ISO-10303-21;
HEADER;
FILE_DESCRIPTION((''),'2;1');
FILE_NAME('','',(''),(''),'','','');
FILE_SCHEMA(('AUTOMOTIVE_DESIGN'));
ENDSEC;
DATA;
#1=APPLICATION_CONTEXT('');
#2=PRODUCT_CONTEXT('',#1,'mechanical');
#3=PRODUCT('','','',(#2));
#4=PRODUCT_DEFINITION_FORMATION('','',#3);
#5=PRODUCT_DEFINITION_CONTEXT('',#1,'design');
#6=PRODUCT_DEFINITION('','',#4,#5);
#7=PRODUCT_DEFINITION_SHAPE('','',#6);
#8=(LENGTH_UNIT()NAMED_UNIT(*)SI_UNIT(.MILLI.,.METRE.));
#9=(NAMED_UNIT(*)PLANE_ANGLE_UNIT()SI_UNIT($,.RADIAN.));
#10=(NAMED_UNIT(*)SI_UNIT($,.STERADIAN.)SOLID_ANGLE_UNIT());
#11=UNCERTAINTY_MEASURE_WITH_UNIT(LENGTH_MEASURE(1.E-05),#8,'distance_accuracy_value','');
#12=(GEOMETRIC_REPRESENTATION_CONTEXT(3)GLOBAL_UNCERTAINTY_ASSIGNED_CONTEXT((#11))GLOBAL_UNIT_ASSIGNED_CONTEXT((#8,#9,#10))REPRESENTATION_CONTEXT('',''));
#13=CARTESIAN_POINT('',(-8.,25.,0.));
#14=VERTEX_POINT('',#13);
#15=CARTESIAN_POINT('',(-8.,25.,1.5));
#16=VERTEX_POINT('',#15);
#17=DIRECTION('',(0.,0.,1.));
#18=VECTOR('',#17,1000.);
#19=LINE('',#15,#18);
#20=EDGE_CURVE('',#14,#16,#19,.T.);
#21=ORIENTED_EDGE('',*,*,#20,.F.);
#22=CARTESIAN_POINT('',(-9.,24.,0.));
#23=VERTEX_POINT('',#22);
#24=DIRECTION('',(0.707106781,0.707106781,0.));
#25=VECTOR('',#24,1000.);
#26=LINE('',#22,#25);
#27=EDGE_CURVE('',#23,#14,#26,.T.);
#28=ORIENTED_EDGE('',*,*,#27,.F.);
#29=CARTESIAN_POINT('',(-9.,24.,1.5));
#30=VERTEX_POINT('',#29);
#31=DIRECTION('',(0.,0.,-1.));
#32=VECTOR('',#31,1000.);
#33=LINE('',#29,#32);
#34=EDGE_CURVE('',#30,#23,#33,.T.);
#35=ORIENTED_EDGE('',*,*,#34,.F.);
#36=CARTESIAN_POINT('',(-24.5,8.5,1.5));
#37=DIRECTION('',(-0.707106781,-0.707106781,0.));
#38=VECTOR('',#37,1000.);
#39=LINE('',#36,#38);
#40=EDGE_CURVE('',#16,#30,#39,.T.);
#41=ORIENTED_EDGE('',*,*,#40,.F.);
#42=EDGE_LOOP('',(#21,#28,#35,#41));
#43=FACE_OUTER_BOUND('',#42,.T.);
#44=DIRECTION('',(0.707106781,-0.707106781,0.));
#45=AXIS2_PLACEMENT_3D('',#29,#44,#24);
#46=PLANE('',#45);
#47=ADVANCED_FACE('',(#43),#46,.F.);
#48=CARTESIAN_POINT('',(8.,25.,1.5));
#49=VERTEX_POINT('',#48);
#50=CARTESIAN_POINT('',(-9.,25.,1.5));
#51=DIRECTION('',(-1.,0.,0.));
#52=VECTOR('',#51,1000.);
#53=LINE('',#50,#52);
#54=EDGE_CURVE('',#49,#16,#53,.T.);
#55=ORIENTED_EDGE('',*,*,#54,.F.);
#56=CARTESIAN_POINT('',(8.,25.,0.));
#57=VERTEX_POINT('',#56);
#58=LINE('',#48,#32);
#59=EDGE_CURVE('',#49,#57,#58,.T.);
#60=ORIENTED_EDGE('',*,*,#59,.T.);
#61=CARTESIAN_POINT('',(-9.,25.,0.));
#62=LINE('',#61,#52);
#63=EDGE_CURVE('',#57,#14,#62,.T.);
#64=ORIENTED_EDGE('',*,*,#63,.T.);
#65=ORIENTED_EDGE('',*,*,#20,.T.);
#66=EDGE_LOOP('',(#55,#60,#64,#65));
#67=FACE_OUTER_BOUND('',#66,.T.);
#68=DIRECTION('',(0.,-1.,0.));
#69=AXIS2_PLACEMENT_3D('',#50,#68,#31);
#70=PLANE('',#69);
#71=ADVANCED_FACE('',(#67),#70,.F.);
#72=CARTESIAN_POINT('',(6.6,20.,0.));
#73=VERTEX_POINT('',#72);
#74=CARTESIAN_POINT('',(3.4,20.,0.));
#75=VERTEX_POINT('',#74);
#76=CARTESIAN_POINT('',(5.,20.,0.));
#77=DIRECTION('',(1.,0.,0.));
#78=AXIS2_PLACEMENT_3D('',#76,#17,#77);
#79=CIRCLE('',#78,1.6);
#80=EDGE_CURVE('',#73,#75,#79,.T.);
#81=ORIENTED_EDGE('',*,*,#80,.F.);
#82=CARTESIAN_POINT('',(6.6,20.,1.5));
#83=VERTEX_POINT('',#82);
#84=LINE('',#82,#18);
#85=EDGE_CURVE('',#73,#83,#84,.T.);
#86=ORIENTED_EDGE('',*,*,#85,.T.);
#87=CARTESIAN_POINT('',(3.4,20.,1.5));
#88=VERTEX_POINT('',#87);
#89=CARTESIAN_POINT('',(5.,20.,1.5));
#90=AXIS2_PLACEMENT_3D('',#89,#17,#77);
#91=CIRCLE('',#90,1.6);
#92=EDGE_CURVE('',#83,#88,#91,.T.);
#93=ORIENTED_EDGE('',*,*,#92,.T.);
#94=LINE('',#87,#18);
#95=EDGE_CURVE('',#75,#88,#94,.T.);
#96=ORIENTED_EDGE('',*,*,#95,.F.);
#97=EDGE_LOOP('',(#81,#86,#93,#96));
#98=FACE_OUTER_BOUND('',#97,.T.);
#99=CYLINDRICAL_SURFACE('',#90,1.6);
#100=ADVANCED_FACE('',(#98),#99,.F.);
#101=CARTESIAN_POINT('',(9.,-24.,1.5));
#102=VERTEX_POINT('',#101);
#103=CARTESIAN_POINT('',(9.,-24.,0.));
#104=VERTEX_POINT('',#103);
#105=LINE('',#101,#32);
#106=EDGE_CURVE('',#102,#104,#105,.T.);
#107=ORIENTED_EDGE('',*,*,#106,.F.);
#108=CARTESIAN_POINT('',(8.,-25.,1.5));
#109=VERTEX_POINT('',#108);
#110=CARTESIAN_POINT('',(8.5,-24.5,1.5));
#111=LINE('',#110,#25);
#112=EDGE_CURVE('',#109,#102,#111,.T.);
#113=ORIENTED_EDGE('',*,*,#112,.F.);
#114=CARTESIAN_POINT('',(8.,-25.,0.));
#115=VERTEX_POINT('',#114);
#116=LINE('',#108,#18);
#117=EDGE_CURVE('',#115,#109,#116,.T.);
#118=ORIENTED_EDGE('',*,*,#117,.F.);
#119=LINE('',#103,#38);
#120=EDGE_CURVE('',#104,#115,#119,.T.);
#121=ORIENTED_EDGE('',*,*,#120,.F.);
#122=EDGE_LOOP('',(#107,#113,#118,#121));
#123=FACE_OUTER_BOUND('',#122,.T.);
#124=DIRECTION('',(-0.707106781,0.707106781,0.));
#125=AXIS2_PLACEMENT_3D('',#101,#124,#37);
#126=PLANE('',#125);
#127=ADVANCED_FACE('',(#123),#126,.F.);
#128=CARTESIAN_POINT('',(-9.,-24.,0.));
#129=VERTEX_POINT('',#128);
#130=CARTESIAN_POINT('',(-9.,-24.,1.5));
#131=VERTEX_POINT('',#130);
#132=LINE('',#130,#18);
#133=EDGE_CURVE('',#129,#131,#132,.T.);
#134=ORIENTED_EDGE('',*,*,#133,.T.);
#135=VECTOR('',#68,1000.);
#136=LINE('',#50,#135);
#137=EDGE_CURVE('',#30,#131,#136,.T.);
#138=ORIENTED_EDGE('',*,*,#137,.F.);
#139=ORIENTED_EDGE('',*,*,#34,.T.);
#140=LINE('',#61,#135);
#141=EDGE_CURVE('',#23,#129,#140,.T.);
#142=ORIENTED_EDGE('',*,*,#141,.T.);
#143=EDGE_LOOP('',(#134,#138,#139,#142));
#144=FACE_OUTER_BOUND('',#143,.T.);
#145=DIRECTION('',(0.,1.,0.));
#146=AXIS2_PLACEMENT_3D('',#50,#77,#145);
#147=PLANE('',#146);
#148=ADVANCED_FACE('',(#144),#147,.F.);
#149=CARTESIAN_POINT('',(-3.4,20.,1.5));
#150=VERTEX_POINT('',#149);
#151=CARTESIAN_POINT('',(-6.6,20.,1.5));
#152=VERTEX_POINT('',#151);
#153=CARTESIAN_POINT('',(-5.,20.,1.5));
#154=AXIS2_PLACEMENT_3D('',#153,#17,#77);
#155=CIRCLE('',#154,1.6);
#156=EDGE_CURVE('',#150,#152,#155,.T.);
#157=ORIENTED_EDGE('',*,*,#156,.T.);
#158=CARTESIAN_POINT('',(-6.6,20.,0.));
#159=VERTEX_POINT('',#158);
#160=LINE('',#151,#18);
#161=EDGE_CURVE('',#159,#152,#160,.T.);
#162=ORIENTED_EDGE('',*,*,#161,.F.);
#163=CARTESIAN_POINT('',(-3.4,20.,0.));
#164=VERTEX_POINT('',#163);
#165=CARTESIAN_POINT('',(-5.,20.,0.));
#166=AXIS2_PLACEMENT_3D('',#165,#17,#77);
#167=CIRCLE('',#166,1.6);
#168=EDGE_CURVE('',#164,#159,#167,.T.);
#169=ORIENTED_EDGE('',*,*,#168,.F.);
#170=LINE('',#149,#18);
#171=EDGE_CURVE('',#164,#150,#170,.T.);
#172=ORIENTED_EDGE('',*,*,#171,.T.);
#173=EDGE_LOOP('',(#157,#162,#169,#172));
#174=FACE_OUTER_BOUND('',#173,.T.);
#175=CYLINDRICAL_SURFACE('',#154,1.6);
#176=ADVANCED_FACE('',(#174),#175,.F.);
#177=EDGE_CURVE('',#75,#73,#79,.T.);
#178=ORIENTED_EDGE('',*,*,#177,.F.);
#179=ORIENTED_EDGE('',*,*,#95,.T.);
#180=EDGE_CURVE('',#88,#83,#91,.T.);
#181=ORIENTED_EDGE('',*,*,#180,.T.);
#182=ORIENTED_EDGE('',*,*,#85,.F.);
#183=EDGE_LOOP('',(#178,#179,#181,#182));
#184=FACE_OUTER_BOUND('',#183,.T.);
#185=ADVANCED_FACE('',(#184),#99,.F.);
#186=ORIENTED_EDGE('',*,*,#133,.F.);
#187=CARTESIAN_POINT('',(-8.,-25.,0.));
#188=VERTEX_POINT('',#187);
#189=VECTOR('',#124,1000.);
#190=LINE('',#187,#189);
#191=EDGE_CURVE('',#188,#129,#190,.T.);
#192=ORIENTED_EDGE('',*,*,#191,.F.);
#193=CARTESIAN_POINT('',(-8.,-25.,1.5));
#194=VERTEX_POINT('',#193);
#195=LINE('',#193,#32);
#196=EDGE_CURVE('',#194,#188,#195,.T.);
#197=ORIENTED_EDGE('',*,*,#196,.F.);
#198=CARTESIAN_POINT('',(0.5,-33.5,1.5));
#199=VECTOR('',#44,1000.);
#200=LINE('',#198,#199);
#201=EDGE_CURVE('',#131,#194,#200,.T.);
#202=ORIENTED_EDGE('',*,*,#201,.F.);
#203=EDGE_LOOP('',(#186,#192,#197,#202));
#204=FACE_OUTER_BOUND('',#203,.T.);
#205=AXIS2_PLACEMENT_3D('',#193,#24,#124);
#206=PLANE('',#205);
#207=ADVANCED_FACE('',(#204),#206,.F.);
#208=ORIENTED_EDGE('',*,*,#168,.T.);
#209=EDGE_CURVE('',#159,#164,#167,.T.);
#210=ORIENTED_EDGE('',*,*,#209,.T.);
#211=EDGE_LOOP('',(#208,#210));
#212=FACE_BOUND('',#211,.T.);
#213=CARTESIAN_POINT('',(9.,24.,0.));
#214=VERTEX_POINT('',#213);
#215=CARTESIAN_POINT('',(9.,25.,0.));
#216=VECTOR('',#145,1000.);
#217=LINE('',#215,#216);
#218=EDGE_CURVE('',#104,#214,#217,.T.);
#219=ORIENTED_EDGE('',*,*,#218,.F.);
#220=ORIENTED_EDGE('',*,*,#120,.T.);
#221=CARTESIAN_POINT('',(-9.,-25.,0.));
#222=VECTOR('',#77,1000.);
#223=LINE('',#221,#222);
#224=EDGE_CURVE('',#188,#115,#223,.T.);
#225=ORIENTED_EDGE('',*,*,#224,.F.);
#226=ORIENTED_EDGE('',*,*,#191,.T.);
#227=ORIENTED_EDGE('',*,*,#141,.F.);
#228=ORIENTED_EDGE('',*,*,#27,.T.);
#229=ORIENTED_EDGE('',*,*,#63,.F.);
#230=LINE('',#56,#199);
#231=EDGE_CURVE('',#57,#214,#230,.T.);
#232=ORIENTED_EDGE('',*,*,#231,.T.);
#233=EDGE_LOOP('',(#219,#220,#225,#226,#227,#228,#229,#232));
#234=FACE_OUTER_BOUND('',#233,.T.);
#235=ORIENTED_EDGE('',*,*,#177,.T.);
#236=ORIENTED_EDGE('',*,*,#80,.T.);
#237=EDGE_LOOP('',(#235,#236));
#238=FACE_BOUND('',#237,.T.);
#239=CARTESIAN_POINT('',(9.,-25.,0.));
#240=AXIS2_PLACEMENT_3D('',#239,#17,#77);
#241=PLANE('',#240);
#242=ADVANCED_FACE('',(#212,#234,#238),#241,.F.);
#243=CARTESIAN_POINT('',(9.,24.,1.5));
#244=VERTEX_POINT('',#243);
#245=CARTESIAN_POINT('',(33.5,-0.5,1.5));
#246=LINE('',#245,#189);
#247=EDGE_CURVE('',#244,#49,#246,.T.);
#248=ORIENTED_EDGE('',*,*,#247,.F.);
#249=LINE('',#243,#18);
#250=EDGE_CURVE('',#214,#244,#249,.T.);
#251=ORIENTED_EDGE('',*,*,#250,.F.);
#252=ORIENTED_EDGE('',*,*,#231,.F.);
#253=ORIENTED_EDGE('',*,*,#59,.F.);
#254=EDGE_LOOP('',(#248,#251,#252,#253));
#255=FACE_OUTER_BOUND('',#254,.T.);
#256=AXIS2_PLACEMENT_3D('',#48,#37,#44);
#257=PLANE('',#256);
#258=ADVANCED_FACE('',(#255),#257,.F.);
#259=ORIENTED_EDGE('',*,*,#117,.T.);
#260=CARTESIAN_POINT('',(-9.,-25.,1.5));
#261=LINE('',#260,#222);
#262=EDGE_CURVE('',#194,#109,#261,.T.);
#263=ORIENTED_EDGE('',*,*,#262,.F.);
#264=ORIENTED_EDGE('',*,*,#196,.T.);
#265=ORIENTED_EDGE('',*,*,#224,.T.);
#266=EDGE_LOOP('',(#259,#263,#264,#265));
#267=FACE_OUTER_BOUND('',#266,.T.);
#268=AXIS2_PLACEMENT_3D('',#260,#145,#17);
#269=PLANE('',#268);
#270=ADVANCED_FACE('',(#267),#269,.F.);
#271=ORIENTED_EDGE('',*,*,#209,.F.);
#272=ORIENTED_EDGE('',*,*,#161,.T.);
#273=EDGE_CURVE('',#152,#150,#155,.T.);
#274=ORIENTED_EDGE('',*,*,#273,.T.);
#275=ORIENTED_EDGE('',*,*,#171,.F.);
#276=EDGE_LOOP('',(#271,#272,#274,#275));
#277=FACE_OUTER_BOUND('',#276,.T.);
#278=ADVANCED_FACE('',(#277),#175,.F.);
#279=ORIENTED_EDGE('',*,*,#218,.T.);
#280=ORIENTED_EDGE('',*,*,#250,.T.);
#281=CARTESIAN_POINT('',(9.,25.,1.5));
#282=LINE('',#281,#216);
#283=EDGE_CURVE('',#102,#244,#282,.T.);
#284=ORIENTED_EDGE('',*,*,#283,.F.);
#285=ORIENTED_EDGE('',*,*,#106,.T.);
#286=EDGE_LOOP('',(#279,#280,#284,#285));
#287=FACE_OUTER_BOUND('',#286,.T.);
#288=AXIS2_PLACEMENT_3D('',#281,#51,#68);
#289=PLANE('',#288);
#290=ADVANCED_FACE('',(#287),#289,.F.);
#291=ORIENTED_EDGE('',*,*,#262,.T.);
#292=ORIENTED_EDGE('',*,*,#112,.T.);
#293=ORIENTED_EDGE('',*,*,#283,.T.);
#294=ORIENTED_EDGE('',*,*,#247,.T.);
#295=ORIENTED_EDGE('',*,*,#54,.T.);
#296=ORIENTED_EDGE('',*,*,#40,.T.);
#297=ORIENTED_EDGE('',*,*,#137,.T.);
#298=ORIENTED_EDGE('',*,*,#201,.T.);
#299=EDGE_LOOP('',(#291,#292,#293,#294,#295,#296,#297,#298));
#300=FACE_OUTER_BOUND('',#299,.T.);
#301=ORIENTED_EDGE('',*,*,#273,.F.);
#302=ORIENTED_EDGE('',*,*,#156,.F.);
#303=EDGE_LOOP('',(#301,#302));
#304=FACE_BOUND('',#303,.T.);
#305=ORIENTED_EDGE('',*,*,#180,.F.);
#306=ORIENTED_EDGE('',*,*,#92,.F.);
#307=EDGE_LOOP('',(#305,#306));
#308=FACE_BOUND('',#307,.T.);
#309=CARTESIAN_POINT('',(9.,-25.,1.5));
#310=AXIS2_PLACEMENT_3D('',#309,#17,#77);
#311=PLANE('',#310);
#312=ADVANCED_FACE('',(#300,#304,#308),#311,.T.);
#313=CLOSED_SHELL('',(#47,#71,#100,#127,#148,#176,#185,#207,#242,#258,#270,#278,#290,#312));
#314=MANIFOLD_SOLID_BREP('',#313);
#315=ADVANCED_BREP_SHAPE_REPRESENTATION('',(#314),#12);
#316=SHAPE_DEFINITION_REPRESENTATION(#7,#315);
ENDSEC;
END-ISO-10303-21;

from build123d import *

# Parameters (mm, degrees)
SKETCH1_W                      = 18
SKETCH1_H                      = 50
BOSS_EXTRUDE1_DEPTH            = 1.5
F_3_2_3_2_DIAMETER_HOLE1_D     = 3.2
F_3_2_3_2_DIAMETER_HOLE1_DEPTH = 12
F_3_2_3_2_DIAMETER_HOLE1_TIP   = 0.96137699
CHAMFER1_SIZE                  = 1


with BuildPart() as part:
    # Sketch1 → Boss-Extrude1 (new body)
    with BuildSketch(Plane.XY):
        Rectangle(SKETCH1_W, SKETCH1_H)
    extrude(amount=BOSS_EXTRUDE1_DEPTH)

    # Ø3.2 (3.2) Diameter Hole1
    with Locations(Plane.XY.offset(1.5)):
        with Locations((-5, 20), (5, 20)):
            Hole(F_3_2_3_2_DIAMETER_HOLE1_D / 2, depth=F_3_2_3_2_DIAMETER_HOLE1_DEPTH)
            with Locations((0, 0, -(F_3_2_3_2_DIAMETER_HOLE1_DEPTH + F_3_2_3_2_DIAMETER_HOLE1_TIP / 2))):  # 118° drill point
                Cone(0, F_3_2_3_2_DIAMETER_HOLE1_D / 2, F_3_2_3_2_DIAMETER_HOLE1_TIP, mode=Mode.SUBTRACT)

    # Chamfer1
    chamfer1_edges = [part.edges().sort_by_distance(p)[0] for p in [
        (9, -25, 0.75),
        (-9, -25, 0.75),
        (-9, 25, 0.75),
        (9, 25, 0.75),
    ]]
    chamfer(chamfer1_edges, length=CHAMFER1_SIZE)


solid = part.part
